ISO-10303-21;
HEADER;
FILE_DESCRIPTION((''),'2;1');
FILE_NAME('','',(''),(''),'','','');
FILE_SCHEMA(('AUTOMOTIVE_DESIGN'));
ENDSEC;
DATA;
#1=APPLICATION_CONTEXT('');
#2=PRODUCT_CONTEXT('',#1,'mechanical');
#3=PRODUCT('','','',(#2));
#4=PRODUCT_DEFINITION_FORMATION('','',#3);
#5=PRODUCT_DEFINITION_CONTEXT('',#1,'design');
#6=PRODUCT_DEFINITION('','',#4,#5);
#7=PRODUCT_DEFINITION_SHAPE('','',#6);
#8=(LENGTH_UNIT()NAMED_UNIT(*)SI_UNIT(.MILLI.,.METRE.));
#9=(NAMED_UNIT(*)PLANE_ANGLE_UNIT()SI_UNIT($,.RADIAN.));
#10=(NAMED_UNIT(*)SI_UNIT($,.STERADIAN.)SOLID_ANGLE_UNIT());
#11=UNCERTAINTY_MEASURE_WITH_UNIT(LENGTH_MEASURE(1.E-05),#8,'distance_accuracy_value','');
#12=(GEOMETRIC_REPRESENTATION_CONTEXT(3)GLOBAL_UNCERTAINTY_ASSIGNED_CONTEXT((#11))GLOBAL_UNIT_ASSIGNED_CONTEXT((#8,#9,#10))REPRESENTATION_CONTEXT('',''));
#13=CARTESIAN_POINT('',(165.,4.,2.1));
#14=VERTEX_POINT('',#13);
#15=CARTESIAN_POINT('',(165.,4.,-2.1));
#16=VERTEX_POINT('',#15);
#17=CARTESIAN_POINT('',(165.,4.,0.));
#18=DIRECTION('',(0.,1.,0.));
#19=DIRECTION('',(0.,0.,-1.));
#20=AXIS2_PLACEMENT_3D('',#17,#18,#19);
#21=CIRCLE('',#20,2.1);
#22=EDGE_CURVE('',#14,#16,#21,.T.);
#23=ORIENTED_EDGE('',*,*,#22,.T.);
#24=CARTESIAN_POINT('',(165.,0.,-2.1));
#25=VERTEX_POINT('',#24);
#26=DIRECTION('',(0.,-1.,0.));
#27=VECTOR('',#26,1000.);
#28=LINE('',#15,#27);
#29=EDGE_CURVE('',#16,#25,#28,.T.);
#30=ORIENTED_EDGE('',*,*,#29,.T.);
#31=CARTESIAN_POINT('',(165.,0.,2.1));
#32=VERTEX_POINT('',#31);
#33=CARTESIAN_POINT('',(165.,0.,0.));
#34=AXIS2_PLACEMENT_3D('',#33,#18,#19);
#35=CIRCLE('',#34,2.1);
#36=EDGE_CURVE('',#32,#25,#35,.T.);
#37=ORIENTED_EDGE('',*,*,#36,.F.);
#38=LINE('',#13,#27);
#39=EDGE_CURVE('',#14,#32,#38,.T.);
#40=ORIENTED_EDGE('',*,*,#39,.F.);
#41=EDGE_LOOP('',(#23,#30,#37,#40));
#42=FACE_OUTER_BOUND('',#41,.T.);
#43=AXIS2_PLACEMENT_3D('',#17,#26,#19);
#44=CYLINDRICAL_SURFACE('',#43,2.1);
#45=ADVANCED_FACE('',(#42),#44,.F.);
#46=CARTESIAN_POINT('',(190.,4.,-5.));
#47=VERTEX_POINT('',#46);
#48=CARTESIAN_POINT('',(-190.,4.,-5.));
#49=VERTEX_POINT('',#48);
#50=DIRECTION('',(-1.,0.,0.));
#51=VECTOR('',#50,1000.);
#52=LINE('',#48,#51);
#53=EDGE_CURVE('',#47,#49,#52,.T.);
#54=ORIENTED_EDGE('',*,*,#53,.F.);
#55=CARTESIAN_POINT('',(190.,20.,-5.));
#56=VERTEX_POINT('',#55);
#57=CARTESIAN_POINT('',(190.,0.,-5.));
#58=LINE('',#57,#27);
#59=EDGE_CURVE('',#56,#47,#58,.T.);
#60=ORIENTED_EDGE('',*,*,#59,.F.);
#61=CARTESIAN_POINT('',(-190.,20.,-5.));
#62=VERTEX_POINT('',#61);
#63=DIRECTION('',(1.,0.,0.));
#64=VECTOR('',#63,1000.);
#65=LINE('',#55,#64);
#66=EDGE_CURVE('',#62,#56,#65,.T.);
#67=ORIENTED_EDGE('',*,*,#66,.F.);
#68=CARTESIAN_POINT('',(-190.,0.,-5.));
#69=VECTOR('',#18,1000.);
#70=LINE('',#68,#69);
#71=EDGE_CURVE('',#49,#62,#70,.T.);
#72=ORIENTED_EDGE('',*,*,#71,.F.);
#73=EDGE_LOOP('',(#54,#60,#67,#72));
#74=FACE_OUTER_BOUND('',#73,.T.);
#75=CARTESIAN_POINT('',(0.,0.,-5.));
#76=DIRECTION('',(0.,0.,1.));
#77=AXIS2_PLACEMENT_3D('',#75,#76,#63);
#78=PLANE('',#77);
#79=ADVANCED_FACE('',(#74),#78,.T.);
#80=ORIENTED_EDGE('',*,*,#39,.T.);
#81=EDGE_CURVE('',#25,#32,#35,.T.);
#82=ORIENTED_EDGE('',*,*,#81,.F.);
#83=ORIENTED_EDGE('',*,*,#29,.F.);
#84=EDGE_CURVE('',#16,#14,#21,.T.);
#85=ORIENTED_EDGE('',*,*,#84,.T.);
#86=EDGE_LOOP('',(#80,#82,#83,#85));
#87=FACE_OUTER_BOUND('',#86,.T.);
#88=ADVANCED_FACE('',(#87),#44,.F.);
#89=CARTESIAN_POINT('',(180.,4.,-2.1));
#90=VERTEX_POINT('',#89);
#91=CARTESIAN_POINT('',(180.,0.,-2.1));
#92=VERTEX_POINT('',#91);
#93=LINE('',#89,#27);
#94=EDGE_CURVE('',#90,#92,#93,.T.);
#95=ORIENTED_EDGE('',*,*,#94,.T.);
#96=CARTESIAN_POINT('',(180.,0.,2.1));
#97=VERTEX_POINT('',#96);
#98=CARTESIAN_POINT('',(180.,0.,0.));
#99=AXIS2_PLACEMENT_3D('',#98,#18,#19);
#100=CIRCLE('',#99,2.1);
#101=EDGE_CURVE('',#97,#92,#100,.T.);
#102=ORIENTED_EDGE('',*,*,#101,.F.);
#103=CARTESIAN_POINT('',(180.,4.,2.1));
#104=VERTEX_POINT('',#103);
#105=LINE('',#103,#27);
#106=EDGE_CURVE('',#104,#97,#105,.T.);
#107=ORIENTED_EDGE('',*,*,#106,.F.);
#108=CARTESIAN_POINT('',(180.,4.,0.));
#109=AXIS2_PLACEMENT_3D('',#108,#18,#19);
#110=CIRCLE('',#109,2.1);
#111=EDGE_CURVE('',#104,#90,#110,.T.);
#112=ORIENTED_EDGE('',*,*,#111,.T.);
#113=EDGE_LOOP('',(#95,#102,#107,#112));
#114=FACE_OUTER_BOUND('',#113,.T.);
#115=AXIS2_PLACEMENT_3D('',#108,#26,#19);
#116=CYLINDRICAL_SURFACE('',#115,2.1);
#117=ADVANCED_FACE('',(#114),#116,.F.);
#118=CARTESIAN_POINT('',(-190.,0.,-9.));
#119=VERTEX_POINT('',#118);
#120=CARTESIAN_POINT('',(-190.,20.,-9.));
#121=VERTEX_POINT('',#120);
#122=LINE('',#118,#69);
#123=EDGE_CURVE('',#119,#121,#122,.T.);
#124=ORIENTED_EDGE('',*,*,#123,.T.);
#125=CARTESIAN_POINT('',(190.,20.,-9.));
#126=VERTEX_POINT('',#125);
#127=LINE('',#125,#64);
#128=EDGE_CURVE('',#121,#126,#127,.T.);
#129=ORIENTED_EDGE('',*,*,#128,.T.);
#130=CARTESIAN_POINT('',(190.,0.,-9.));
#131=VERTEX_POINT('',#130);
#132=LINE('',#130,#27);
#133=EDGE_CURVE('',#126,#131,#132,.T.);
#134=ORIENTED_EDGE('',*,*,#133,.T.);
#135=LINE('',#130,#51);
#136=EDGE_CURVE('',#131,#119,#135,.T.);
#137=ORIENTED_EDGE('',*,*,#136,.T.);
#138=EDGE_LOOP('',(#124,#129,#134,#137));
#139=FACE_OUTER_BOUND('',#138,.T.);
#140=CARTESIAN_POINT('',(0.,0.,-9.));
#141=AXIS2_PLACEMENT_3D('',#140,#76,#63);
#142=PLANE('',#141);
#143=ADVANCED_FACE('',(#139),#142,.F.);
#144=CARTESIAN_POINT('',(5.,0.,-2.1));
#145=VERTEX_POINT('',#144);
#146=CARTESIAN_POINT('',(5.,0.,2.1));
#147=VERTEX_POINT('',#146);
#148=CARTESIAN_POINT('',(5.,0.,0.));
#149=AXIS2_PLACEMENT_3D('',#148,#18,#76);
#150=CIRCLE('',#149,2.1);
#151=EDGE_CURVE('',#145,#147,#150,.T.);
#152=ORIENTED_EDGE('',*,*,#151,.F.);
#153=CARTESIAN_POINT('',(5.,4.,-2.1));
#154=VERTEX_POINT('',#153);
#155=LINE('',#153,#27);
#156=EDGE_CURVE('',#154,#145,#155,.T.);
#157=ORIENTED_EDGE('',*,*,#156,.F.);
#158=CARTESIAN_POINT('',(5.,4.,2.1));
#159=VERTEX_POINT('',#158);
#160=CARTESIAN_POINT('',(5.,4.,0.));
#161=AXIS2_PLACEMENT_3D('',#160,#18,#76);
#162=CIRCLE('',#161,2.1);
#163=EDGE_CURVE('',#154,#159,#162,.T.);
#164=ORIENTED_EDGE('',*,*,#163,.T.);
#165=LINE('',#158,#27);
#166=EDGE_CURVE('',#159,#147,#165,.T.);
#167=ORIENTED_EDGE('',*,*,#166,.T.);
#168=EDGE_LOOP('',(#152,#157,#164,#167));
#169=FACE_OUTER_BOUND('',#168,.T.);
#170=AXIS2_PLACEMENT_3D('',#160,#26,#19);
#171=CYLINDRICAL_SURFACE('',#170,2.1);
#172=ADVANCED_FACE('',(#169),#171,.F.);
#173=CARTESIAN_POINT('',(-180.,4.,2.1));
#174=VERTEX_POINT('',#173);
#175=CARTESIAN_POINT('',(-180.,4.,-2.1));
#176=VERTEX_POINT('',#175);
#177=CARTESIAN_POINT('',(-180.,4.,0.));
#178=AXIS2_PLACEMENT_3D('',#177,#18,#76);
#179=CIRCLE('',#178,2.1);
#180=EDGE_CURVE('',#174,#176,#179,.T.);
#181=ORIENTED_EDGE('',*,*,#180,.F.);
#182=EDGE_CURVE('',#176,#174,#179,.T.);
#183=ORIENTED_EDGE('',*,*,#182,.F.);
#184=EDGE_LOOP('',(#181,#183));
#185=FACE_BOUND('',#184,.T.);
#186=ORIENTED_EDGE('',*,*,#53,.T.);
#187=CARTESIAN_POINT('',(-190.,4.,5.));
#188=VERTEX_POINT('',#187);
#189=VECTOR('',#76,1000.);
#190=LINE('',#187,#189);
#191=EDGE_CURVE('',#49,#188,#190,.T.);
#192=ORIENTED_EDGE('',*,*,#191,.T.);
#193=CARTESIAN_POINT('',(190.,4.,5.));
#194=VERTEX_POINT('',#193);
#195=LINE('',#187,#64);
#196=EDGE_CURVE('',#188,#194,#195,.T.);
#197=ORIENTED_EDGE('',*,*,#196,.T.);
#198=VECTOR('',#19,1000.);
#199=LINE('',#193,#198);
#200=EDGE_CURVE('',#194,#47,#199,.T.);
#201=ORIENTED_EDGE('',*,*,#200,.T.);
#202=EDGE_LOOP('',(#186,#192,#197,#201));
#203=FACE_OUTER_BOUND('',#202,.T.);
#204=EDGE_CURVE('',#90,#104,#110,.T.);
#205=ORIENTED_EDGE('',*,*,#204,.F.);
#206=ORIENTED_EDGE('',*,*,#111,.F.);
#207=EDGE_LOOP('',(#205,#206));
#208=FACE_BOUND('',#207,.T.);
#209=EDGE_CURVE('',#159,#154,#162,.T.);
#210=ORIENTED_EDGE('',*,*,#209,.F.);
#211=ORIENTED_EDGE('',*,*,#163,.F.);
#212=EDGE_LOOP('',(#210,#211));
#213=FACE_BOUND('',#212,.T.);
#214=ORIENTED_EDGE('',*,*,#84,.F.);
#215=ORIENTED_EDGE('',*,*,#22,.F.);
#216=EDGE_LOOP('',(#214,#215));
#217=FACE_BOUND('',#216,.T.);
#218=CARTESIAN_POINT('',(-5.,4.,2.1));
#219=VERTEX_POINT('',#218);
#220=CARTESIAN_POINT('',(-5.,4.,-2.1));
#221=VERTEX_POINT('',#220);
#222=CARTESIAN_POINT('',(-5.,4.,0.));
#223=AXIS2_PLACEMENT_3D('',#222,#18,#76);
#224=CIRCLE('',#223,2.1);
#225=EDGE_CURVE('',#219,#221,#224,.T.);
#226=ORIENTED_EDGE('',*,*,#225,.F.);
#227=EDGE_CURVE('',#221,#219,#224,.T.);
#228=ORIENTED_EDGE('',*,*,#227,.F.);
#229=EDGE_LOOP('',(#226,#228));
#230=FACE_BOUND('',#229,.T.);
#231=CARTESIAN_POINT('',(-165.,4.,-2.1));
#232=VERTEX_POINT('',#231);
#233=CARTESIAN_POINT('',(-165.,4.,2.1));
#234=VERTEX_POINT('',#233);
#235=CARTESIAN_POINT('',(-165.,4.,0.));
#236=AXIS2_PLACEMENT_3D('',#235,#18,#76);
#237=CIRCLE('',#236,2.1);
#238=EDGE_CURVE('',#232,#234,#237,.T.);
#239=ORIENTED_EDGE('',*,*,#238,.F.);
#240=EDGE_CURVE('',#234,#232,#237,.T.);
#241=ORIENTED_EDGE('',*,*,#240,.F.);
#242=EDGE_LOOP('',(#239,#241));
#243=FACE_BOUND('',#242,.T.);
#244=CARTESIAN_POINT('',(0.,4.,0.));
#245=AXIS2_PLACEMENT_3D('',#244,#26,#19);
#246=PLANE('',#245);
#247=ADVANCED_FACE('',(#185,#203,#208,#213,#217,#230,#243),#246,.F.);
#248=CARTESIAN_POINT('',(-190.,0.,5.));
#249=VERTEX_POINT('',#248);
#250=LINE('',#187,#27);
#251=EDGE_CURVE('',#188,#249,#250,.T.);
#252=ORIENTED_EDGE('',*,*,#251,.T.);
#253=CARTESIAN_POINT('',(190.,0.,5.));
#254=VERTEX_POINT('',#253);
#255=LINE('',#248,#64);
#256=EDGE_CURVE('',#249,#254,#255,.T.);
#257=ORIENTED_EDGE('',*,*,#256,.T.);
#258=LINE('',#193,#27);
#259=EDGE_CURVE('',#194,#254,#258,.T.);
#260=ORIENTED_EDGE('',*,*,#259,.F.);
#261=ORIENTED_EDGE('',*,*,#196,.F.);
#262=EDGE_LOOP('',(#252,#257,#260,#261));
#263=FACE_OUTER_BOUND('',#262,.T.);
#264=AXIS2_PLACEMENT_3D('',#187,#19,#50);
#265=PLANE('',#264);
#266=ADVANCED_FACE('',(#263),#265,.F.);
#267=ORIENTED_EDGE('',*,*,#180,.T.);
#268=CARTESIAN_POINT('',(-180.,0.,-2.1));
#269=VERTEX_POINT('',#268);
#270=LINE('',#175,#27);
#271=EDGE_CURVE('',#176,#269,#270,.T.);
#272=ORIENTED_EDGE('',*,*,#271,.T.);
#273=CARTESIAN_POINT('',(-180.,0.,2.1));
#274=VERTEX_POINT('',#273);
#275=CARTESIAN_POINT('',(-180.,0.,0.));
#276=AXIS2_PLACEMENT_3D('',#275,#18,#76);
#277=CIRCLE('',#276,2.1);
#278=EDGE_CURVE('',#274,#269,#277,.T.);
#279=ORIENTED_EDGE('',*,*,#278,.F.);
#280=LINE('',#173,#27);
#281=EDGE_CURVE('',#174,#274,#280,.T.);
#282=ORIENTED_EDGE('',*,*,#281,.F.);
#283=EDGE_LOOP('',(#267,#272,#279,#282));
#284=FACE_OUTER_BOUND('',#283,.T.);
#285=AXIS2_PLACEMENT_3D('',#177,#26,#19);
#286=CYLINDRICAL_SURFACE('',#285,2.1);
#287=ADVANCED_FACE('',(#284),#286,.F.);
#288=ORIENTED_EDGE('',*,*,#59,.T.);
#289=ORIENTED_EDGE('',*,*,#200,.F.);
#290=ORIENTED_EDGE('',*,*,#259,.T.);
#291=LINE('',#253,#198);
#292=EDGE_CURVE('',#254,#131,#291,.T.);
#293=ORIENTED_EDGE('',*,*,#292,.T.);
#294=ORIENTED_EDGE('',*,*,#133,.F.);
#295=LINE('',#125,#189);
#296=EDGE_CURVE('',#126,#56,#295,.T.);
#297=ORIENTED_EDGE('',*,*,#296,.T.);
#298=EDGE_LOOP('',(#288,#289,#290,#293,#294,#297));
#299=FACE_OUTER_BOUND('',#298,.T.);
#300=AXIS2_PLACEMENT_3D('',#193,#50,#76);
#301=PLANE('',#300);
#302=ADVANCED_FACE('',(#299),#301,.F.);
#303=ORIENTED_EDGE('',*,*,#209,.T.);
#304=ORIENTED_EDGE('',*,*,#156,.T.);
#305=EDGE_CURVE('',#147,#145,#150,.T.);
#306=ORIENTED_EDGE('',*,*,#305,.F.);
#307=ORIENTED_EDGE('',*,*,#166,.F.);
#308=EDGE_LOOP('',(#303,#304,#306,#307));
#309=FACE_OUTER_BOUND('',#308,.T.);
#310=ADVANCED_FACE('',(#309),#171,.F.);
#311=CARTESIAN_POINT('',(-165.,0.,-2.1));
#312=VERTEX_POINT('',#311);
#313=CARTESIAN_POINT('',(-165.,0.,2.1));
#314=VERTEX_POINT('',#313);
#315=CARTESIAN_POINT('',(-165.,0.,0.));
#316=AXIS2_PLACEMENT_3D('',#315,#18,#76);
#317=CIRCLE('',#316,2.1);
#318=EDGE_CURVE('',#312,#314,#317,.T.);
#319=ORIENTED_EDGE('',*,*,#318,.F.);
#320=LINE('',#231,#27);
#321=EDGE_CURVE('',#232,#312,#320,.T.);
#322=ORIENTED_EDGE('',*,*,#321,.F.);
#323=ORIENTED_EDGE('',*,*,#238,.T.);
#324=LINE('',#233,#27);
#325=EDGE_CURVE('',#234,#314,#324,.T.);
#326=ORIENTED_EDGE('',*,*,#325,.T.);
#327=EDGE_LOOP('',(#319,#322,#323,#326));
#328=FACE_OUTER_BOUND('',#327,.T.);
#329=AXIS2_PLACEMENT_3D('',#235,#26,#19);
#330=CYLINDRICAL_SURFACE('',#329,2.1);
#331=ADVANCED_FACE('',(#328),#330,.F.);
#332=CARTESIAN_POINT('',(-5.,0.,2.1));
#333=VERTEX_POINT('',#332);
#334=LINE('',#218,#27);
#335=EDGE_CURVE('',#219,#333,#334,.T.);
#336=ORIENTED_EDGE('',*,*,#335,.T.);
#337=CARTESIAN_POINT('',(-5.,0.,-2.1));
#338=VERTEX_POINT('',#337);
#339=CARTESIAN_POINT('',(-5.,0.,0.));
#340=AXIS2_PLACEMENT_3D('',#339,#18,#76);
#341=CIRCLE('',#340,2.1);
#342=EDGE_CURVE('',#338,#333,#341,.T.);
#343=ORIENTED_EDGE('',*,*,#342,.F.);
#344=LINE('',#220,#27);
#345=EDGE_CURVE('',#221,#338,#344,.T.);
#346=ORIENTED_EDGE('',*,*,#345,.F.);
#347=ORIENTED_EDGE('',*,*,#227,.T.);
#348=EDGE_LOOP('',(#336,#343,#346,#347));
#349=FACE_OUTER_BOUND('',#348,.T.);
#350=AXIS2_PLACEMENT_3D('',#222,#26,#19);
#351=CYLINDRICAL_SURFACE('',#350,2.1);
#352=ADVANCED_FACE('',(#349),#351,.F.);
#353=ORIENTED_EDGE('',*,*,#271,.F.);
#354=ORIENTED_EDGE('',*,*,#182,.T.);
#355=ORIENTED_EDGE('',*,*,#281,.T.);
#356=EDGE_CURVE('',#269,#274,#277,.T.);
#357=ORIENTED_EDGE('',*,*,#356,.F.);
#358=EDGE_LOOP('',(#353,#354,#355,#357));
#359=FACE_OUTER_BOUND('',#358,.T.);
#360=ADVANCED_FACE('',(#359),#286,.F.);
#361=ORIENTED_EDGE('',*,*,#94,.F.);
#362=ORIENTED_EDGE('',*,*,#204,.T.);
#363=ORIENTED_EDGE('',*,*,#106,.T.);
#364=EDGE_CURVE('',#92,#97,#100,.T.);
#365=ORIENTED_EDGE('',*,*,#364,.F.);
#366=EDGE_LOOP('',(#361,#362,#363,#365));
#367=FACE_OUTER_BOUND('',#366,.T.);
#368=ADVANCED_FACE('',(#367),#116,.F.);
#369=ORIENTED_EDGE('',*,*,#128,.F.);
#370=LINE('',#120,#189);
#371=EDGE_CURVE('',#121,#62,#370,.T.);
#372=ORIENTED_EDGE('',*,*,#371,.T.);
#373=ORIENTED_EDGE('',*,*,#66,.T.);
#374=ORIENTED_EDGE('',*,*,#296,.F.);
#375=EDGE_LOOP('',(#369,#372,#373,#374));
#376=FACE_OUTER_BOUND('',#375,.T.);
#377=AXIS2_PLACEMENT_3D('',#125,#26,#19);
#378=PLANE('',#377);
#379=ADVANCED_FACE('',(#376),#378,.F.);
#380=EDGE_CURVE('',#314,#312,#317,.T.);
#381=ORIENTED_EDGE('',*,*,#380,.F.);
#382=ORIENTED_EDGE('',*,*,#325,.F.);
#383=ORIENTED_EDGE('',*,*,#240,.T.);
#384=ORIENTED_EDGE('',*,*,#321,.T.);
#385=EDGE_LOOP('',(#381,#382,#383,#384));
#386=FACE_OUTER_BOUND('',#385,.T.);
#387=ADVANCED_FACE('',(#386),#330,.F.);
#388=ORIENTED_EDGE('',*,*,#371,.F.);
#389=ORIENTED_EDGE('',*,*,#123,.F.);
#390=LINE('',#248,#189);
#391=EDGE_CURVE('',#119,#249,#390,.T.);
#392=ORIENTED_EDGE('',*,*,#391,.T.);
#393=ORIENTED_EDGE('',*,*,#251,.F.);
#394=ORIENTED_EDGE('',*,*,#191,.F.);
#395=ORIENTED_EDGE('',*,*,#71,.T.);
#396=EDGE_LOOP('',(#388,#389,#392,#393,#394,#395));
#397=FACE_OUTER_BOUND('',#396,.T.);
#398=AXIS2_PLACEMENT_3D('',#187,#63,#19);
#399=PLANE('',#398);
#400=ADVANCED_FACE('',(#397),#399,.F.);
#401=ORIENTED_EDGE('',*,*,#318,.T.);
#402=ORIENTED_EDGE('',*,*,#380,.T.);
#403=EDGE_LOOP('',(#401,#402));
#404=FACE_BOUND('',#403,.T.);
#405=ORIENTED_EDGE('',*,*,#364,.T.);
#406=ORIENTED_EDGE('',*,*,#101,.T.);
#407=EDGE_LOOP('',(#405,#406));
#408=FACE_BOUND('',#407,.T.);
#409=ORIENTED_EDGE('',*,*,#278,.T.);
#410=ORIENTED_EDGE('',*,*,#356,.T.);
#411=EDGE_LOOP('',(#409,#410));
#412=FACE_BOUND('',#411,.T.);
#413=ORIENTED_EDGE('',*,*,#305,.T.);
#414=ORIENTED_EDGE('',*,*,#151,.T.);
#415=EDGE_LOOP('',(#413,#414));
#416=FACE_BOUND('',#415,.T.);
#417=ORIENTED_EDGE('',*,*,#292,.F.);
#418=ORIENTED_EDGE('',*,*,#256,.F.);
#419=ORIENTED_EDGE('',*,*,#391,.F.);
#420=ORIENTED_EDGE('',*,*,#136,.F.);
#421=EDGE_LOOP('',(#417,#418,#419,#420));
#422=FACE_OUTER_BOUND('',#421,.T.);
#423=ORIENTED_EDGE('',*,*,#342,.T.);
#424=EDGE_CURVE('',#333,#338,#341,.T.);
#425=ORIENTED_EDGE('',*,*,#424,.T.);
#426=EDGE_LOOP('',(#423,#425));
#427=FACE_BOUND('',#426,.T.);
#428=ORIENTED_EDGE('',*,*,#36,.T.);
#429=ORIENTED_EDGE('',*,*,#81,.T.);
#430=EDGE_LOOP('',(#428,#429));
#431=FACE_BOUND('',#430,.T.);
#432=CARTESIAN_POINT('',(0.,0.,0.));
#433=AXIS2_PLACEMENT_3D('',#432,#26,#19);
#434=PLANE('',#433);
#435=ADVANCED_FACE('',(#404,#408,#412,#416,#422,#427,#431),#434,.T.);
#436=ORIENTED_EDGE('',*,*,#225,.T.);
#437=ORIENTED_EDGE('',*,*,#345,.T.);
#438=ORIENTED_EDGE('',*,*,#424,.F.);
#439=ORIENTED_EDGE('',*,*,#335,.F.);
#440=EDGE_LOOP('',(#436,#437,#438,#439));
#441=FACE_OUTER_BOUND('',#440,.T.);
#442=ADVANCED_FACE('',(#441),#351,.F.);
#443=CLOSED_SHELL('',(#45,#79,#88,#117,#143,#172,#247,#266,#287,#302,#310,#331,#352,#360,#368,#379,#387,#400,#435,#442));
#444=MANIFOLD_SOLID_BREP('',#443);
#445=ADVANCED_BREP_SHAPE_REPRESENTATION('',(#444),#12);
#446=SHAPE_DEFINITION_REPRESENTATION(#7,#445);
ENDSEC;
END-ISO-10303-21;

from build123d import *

# Parameters (mm, degrees)
SKETCH1_W           = 380
SKETCH1_H           = 10
SKETCH1_R           = 2.1
BOSS_EXTRUDE1_DEPTH = 4
SKETCH2_W           = 380
SKETCH2_H           = 20
BOSS_EXTRUDE2_DEPTH = 4


with BuildPart() as part:
    # Sketch1 → Boss-Extrude1 (new body)
    with BuildSketch(Plane(origin=(0, 0, 0), x_dir=(1, 0, 0), z_dir=(0, 1, 0))):
        Rectangle(SKETCH1_W, SKETCH1_H)
        with Locations(Location((-180, 0, 0), (0, 0, 270))):
            Circle(SKETCH1_R, mode=Mode.SUBTRACT)
        with Locations(Location((-165, 0, 0), (0, 0, 270))):
            Circle(SKETCH1_R, mode=Mode.SUBTRACT)
        with Locations(Location((165, 0, 0), (0, 0, 90))):
            Circle(SKETCH1_R, mode=Mode.SUBTRACT)
        with Locations(Location((180, 0, 0), (0, 0, 90))):
            Circle(SKETCH1_R, mode=Mode.SUBTRACT)
        with Locations(Location((5, 0, 0), (0, 0, 270))):
            Circle(SKETCH1_R, mode=Mode.SUBTRACT)
        with Locations(Location((-5, 0, 0), (0, 0, 270))):
            Circle(SKETCH1_R, mode=Mode.SUBTRACT)
    extrude(amount=BOSS_EXTRUDE1_DEPTH)

    # Sketch2 → Boss-Extrude2 (add)
    with BuildSketch(Plane(origin=(0, 0, -5), x_dir=(-1, 0, 0), z_dir=(0, 0, -1))):
        with Locations((0, 10)):
            Rectangle(SKETCH2_W, SKETCH2_H)
    extrude(amount=BOSS_EXTRUDE2_DEPTH)


solid = part.part
